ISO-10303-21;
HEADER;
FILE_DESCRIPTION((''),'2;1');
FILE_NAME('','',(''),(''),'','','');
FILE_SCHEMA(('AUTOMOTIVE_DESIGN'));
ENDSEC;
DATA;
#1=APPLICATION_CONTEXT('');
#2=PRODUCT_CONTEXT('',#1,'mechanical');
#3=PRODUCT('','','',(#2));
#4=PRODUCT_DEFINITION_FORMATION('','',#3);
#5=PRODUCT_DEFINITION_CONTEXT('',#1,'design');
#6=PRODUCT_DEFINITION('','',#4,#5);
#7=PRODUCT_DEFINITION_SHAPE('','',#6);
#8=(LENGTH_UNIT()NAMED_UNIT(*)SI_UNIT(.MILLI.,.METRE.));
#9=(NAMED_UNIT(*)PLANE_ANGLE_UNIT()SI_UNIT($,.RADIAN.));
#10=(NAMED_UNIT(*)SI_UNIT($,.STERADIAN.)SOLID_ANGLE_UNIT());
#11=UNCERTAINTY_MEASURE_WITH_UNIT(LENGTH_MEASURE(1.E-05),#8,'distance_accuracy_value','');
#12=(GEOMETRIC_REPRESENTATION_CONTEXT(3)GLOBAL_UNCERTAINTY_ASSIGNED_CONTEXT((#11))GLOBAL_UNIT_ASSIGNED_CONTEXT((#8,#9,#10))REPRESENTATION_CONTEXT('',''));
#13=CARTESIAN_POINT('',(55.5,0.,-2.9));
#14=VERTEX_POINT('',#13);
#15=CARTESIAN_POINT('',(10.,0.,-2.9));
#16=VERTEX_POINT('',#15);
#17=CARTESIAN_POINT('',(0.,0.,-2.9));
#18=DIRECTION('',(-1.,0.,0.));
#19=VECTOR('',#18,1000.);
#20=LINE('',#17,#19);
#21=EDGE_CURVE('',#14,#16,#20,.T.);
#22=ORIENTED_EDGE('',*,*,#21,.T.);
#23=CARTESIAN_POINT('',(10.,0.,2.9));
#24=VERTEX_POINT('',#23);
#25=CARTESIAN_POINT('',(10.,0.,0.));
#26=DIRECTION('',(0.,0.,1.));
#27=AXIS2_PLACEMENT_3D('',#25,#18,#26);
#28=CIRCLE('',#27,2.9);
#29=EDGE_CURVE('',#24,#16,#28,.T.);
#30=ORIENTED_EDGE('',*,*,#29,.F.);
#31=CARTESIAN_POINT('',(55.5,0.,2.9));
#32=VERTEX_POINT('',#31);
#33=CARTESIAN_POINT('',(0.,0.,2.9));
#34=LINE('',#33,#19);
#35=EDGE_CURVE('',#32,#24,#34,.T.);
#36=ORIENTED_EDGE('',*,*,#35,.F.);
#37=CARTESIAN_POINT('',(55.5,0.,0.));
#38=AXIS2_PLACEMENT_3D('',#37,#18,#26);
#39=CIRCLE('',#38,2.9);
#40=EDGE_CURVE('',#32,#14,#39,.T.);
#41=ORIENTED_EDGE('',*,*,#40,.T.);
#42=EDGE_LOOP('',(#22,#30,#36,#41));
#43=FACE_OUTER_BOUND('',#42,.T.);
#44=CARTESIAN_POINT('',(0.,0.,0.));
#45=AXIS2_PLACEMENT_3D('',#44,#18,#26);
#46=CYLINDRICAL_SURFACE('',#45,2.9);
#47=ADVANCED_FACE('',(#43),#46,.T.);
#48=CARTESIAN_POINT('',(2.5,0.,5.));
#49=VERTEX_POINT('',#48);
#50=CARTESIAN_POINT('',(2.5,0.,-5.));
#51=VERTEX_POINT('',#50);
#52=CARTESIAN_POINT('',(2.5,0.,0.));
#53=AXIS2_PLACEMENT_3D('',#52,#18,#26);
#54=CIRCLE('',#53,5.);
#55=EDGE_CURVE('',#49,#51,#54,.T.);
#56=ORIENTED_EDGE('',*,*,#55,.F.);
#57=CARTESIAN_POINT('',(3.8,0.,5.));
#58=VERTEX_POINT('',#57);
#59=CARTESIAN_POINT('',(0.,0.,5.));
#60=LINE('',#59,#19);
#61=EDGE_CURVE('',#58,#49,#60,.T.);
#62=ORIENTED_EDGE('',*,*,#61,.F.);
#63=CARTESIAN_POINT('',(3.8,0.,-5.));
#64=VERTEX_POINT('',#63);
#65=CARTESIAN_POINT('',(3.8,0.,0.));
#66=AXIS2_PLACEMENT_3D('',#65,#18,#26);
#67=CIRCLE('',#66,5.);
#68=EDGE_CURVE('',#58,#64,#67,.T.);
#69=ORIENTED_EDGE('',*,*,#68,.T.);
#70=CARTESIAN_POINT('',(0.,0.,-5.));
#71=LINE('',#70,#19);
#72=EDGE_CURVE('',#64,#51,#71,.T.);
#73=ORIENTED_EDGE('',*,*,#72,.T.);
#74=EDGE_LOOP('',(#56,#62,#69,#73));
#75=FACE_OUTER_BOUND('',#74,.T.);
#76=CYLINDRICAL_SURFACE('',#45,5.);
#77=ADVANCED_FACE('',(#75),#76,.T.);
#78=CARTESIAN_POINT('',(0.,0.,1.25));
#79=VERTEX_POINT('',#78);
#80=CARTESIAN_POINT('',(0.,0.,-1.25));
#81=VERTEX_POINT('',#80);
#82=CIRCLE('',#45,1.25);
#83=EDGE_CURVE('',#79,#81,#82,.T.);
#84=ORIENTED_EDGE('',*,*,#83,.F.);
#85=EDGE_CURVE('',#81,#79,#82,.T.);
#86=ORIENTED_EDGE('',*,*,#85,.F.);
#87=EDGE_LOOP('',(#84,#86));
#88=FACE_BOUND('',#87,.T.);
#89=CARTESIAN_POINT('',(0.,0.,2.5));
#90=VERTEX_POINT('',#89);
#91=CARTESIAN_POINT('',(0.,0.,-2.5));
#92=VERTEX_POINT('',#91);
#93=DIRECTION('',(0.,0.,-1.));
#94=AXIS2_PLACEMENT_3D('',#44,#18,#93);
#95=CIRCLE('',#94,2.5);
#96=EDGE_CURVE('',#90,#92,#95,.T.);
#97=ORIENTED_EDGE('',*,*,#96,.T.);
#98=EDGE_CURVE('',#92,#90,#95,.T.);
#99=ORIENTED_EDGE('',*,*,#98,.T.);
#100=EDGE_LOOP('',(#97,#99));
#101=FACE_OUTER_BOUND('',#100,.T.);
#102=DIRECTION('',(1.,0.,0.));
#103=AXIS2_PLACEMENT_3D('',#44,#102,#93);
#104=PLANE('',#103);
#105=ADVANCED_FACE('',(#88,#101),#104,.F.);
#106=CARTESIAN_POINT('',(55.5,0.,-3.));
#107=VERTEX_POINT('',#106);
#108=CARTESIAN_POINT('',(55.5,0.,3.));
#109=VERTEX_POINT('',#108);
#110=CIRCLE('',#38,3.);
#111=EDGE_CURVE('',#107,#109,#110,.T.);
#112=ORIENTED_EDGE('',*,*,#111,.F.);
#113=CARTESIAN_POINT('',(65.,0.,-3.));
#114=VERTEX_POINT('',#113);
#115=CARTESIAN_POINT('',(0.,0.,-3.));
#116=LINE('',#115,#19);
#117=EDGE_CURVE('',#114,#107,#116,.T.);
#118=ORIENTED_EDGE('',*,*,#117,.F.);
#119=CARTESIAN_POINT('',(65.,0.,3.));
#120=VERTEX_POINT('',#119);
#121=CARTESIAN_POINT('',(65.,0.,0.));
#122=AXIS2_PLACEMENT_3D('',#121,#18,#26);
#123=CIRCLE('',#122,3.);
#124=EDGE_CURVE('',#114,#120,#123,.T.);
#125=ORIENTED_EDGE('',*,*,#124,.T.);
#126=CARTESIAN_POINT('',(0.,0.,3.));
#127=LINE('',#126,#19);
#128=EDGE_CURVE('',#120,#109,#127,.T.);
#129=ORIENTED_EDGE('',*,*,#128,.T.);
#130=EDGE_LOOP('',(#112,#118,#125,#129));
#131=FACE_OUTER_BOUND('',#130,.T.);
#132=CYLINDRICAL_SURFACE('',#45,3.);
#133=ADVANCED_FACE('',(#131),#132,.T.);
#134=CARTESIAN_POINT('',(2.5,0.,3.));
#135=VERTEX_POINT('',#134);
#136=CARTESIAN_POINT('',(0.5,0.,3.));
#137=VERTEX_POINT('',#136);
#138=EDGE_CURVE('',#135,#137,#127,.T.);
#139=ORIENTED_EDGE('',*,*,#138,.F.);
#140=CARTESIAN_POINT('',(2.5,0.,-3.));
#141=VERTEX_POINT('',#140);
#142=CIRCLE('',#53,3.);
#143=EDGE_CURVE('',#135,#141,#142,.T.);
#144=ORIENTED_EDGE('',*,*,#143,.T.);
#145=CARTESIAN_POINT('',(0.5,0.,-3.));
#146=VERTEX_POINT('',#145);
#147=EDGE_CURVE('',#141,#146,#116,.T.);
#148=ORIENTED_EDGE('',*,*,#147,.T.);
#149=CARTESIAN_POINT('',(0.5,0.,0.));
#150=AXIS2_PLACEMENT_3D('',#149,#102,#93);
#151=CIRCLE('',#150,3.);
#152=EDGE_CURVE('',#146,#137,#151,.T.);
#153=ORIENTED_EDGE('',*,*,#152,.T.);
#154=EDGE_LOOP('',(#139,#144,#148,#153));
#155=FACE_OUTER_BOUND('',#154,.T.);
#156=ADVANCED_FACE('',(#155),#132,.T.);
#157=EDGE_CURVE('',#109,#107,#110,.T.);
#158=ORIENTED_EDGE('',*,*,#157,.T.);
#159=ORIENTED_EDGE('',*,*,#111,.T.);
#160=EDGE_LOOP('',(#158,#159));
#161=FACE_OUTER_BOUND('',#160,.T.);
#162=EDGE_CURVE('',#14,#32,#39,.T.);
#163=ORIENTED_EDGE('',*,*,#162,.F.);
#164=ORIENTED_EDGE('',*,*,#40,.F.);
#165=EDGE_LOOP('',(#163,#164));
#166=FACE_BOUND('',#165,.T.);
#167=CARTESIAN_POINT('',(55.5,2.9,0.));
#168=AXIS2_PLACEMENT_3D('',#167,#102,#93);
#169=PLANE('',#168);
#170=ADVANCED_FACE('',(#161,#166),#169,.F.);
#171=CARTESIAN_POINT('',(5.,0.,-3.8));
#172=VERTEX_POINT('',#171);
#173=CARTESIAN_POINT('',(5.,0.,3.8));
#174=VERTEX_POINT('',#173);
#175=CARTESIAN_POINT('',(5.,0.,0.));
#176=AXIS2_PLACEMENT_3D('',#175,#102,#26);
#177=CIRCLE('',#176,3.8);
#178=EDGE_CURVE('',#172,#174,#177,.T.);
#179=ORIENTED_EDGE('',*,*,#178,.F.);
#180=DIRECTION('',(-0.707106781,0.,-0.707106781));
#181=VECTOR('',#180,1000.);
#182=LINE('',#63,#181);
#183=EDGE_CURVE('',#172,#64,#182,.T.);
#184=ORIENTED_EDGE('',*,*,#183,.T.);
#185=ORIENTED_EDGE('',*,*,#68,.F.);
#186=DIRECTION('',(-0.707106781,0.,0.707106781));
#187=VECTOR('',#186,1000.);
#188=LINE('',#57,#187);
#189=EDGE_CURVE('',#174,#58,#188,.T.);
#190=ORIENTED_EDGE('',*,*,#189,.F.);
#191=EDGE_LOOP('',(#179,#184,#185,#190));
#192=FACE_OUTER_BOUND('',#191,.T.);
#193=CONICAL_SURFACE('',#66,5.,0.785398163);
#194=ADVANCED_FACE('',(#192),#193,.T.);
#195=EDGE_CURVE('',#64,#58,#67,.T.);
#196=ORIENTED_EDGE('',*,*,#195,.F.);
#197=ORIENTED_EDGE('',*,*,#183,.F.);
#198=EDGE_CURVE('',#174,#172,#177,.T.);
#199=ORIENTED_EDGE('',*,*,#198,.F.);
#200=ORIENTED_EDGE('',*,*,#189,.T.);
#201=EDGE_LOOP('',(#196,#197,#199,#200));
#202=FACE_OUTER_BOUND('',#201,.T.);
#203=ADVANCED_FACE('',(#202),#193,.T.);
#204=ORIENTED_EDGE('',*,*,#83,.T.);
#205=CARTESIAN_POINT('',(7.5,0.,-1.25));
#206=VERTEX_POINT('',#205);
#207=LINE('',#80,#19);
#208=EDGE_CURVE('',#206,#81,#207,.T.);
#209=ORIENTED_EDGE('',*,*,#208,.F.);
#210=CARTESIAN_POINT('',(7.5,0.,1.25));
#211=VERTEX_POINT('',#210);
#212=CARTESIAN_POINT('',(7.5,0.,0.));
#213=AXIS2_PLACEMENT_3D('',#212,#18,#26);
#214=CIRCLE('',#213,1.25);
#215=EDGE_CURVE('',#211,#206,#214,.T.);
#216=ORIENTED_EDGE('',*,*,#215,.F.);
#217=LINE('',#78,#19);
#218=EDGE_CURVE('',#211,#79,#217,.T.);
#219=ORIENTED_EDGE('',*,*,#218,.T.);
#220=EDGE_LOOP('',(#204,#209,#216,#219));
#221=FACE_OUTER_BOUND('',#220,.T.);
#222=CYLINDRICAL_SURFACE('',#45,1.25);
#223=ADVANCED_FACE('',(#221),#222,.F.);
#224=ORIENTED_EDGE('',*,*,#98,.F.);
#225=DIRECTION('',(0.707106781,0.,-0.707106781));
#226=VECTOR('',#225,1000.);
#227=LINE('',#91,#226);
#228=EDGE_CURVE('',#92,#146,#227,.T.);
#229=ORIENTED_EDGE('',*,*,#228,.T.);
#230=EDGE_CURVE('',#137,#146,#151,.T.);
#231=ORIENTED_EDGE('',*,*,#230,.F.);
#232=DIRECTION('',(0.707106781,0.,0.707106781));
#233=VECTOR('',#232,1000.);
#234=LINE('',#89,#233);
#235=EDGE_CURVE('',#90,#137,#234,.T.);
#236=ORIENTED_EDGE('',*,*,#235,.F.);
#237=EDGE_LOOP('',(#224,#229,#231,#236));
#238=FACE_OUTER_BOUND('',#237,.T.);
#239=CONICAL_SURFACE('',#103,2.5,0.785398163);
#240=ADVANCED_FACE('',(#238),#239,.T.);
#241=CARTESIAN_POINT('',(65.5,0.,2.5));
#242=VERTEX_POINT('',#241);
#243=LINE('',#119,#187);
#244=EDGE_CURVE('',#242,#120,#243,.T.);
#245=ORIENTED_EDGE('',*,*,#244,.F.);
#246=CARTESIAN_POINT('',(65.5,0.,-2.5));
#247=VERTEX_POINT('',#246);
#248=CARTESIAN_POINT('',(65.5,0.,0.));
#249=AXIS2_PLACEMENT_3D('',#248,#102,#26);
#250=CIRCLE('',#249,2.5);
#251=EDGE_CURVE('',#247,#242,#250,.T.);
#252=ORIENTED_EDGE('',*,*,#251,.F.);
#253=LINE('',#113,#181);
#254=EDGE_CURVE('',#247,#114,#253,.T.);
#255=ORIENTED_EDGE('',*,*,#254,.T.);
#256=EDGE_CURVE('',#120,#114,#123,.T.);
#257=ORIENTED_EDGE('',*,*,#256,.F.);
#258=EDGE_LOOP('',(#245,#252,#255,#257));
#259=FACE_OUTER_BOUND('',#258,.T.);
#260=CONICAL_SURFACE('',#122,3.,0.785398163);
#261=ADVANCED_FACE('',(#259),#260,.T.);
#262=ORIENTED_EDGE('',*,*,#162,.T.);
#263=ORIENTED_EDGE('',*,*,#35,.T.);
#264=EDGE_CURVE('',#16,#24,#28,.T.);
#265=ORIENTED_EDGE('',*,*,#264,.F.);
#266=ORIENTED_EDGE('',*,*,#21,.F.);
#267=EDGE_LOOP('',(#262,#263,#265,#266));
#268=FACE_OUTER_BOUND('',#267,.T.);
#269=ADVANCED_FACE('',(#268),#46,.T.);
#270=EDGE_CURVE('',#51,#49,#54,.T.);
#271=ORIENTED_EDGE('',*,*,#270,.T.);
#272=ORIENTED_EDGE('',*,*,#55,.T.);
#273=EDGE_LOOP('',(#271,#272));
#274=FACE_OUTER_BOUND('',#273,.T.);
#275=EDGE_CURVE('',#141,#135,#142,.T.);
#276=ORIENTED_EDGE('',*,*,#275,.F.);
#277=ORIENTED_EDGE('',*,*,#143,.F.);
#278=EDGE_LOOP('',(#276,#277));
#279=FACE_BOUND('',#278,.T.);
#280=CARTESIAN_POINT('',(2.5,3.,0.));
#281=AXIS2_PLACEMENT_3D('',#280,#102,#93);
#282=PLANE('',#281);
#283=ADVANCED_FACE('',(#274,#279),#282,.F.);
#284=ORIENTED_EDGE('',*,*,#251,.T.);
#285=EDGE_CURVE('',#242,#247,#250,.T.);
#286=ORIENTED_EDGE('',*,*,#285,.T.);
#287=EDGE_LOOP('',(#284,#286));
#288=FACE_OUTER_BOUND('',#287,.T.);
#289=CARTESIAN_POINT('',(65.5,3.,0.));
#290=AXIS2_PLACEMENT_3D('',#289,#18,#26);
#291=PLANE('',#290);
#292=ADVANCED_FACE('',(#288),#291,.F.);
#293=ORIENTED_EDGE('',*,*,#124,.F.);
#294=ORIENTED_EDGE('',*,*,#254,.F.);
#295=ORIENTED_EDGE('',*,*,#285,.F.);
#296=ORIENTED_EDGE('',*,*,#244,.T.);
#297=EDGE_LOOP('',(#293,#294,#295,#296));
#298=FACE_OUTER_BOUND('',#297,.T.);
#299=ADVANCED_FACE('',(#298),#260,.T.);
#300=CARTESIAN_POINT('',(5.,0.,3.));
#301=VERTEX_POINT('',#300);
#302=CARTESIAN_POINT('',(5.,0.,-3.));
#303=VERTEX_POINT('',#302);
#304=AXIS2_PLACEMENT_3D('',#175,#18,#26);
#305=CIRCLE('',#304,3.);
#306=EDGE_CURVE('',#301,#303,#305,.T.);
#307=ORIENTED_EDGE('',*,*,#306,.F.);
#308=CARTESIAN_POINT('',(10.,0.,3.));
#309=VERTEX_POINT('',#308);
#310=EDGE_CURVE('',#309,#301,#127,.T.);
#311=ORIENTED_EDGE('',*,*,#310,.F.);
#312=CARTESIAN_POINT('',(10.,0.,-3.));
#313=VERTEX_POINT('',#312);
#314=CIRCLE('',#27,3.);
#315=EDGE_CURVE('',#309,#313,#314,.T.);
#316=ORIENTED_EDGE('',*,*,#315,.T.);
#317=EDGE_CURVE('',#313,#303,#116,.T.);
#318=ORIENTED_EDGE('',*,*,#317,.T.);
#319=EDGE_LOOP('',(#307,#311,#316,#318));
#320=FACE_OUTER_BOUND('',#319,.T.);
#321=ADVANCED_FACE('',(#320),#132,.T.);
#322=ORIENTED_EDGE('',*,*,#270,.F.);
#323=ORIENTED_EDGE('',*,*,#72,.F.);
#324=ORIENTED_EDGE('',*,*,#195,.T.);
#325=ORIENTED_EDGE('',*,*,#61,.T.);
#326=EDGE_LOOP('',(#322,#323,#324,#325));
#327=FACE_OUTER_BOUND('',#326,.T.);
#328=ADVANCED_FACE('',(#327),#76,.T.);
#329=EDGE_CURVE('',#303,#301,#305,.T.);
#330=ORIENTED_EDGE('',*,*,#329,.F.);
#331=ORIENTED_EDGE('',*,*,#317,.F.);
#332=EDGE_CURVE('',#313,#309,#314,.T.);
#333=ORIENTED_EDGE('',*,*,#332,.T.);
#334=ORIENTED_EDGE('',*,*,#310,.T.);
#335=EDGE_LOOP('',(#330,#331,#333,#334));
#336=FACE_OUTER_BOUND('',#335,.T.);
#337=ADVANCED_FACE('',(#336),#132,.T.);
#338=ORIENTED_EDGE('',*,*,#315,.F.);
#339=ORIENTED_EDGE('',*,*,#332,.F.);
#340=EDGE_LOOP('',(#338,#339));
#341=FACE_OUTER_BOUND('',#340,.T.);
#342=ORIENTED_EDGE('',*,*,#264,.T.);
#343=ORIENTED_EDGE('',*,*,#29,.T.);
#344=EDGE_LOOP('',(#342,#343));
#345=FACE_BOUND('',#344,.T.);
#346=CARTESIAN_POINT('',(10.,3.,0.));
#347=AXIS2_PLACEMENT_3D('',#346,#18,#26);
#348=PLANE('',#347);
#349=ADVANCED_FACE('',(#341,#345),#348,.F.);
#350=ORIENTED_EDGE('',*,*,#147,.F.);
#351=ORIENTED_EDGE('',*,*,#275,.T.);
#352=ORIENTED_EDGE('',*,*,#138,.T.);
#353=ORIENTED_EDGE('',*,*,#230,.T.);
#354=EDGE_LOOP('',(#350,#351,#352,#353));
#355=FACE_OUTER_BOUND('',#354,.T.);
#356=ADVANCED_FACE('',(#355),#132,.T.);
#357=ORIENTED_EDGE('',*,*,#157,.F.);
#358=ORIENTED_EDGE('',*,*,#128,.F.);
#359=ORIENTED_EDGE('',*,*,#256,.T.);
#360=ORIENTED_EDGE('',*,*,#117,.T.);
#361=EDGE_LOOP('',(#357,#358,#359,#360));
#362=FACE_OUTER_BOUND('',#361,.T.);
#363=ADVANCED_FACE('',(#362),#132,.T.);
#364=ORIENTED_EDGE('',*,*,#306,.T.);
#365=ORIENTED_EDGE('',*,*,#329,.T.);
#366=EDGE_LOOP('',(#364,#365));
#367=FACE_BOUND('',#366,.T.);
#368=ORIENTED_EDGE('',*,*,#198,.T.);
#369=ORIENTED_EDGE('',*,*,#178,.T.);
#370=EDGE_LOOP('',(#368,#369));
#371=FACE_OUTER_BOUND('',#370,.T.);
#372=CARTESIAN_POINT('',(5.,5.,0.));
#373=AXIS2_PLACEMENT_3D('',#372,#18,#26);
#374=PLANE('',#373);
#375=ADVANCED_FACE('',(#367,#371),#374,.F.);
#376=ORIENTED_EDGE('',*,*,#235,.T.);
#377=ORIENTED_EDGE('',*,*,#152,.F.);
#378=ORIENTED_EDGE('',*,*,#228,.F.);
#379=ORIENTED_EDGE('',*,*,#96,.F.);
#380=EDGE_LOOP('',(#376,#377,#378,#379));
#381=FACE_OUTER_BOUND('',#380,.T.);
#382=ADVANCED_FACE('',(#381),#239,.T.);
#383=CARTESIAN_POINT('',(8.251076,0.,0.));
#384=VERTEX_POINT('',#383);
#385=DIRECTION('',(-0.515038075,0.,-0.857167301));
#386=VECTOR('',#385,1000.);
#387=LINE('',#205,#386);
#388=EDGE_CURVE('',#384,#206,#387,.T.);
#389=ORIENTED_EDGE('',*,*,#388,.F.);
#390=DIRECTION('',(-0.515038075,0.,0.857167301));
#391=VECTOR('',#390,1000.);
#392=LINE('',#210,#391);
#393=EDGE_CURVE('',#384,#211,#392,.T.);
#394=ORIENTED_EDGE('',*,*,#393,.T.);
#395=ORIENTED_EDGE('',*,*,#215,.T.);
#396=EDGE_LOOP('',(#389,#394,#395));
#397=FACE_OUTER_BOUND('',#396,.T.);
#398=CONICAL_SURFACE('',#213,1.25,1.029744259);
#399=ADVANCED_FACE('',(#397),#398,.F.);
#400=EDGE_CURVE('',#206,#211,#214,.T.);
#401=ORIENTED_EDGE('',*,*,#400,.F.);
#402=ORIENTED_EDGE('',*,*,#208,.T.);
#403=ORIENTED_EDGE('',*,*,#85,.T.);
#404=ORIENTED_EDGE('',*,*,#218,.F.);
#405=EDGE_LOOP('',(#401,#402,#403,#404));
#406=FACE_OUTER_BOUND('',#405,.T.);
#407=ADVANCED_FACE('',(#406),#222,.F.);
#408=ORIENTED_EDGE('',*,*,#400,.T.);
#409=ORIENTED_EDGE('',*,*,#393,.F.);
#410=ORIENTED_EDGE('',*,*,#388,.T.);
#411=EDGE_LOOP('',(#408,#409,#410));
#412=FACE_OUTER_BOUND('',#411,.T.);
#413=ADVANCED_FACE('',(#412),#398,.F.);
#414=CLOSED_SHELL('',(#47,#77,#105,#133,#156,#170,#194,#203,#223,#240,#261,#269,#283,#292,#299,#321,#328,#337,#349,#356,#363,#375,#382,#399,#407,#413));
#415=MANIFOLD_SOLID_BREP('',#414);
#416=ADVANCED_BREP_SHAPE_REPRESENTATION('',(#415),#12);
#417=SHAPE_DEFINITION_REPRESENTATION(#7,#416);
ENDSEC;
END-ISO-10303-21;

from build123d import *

# Parameters (mm, degrees)
CHAMFER1_SIZE         = 1.2
M3_TAPPED_HOLE1_D     = 2.5
M3_TAPPED_HOLE1_DEPTH = 7.5
M3_TAPPED_HOLE1_TIP   = 0.751075774
CHAMFER2_SIZE         = 0.5


with BuildPart() as part:
    # Sketch1 → Revolve1 (revolve)
    with BuildSketch(Plane.XY, mode=Mode.PRIVATE) as revolve1_sk:
        Polygon((0, 0), (0, 3), (2.5, 3), (2.5, 5), (5, 5), (5, 3), (10, 3), (10, 2.9), (55.5, 2.9), (55.5, 3), (65.5, 3), (65.5, 0), align=None)
    revolve(revolve1_sk.sketch.rotate(Axis((0, 0, 0), (1, 0, 0)), 90), axis=Axis((0, 0, 0), (1, 0, 0)))

    # Chamfer1
    chamfer1_edges = [part.edges().sort_by_distance(p)[0] for p in [
        (5, 0, -5),
    ]]
    chamfer(chamfer1_edges, length=CHAMFER1_SIZE)

    # M3 Tapped Hole1
    with Locations(Plane.ZY):
        with Locations((0, 0)):
            Hole(M3_TAPPED_HOLE1_D / 2, depth=M3_TAPPED_HOLE1_DEPTH)
            with Locations((0, 0, -(M3_TAPPED_HOLE1_DEPTH + M3_TAPPED_HOLE1_TIP / 2))):  # 118° drill point
                Cone(0, M3_TAPPED_HOLE1_D / 2, M3_TAPPED_HOLE1_TIP, mode=Mode.SUBTRACT)

    # Chamfer2
    chamfer2_edges = [part.edges().sort_by_distance(p)[0] for p in [
        (0, 0, -3),
        (65.5, 0, -3),
    ]]
    chamfer(chamfer2_edges, length=CHAMFER2_SIZE)


solid = part.part
